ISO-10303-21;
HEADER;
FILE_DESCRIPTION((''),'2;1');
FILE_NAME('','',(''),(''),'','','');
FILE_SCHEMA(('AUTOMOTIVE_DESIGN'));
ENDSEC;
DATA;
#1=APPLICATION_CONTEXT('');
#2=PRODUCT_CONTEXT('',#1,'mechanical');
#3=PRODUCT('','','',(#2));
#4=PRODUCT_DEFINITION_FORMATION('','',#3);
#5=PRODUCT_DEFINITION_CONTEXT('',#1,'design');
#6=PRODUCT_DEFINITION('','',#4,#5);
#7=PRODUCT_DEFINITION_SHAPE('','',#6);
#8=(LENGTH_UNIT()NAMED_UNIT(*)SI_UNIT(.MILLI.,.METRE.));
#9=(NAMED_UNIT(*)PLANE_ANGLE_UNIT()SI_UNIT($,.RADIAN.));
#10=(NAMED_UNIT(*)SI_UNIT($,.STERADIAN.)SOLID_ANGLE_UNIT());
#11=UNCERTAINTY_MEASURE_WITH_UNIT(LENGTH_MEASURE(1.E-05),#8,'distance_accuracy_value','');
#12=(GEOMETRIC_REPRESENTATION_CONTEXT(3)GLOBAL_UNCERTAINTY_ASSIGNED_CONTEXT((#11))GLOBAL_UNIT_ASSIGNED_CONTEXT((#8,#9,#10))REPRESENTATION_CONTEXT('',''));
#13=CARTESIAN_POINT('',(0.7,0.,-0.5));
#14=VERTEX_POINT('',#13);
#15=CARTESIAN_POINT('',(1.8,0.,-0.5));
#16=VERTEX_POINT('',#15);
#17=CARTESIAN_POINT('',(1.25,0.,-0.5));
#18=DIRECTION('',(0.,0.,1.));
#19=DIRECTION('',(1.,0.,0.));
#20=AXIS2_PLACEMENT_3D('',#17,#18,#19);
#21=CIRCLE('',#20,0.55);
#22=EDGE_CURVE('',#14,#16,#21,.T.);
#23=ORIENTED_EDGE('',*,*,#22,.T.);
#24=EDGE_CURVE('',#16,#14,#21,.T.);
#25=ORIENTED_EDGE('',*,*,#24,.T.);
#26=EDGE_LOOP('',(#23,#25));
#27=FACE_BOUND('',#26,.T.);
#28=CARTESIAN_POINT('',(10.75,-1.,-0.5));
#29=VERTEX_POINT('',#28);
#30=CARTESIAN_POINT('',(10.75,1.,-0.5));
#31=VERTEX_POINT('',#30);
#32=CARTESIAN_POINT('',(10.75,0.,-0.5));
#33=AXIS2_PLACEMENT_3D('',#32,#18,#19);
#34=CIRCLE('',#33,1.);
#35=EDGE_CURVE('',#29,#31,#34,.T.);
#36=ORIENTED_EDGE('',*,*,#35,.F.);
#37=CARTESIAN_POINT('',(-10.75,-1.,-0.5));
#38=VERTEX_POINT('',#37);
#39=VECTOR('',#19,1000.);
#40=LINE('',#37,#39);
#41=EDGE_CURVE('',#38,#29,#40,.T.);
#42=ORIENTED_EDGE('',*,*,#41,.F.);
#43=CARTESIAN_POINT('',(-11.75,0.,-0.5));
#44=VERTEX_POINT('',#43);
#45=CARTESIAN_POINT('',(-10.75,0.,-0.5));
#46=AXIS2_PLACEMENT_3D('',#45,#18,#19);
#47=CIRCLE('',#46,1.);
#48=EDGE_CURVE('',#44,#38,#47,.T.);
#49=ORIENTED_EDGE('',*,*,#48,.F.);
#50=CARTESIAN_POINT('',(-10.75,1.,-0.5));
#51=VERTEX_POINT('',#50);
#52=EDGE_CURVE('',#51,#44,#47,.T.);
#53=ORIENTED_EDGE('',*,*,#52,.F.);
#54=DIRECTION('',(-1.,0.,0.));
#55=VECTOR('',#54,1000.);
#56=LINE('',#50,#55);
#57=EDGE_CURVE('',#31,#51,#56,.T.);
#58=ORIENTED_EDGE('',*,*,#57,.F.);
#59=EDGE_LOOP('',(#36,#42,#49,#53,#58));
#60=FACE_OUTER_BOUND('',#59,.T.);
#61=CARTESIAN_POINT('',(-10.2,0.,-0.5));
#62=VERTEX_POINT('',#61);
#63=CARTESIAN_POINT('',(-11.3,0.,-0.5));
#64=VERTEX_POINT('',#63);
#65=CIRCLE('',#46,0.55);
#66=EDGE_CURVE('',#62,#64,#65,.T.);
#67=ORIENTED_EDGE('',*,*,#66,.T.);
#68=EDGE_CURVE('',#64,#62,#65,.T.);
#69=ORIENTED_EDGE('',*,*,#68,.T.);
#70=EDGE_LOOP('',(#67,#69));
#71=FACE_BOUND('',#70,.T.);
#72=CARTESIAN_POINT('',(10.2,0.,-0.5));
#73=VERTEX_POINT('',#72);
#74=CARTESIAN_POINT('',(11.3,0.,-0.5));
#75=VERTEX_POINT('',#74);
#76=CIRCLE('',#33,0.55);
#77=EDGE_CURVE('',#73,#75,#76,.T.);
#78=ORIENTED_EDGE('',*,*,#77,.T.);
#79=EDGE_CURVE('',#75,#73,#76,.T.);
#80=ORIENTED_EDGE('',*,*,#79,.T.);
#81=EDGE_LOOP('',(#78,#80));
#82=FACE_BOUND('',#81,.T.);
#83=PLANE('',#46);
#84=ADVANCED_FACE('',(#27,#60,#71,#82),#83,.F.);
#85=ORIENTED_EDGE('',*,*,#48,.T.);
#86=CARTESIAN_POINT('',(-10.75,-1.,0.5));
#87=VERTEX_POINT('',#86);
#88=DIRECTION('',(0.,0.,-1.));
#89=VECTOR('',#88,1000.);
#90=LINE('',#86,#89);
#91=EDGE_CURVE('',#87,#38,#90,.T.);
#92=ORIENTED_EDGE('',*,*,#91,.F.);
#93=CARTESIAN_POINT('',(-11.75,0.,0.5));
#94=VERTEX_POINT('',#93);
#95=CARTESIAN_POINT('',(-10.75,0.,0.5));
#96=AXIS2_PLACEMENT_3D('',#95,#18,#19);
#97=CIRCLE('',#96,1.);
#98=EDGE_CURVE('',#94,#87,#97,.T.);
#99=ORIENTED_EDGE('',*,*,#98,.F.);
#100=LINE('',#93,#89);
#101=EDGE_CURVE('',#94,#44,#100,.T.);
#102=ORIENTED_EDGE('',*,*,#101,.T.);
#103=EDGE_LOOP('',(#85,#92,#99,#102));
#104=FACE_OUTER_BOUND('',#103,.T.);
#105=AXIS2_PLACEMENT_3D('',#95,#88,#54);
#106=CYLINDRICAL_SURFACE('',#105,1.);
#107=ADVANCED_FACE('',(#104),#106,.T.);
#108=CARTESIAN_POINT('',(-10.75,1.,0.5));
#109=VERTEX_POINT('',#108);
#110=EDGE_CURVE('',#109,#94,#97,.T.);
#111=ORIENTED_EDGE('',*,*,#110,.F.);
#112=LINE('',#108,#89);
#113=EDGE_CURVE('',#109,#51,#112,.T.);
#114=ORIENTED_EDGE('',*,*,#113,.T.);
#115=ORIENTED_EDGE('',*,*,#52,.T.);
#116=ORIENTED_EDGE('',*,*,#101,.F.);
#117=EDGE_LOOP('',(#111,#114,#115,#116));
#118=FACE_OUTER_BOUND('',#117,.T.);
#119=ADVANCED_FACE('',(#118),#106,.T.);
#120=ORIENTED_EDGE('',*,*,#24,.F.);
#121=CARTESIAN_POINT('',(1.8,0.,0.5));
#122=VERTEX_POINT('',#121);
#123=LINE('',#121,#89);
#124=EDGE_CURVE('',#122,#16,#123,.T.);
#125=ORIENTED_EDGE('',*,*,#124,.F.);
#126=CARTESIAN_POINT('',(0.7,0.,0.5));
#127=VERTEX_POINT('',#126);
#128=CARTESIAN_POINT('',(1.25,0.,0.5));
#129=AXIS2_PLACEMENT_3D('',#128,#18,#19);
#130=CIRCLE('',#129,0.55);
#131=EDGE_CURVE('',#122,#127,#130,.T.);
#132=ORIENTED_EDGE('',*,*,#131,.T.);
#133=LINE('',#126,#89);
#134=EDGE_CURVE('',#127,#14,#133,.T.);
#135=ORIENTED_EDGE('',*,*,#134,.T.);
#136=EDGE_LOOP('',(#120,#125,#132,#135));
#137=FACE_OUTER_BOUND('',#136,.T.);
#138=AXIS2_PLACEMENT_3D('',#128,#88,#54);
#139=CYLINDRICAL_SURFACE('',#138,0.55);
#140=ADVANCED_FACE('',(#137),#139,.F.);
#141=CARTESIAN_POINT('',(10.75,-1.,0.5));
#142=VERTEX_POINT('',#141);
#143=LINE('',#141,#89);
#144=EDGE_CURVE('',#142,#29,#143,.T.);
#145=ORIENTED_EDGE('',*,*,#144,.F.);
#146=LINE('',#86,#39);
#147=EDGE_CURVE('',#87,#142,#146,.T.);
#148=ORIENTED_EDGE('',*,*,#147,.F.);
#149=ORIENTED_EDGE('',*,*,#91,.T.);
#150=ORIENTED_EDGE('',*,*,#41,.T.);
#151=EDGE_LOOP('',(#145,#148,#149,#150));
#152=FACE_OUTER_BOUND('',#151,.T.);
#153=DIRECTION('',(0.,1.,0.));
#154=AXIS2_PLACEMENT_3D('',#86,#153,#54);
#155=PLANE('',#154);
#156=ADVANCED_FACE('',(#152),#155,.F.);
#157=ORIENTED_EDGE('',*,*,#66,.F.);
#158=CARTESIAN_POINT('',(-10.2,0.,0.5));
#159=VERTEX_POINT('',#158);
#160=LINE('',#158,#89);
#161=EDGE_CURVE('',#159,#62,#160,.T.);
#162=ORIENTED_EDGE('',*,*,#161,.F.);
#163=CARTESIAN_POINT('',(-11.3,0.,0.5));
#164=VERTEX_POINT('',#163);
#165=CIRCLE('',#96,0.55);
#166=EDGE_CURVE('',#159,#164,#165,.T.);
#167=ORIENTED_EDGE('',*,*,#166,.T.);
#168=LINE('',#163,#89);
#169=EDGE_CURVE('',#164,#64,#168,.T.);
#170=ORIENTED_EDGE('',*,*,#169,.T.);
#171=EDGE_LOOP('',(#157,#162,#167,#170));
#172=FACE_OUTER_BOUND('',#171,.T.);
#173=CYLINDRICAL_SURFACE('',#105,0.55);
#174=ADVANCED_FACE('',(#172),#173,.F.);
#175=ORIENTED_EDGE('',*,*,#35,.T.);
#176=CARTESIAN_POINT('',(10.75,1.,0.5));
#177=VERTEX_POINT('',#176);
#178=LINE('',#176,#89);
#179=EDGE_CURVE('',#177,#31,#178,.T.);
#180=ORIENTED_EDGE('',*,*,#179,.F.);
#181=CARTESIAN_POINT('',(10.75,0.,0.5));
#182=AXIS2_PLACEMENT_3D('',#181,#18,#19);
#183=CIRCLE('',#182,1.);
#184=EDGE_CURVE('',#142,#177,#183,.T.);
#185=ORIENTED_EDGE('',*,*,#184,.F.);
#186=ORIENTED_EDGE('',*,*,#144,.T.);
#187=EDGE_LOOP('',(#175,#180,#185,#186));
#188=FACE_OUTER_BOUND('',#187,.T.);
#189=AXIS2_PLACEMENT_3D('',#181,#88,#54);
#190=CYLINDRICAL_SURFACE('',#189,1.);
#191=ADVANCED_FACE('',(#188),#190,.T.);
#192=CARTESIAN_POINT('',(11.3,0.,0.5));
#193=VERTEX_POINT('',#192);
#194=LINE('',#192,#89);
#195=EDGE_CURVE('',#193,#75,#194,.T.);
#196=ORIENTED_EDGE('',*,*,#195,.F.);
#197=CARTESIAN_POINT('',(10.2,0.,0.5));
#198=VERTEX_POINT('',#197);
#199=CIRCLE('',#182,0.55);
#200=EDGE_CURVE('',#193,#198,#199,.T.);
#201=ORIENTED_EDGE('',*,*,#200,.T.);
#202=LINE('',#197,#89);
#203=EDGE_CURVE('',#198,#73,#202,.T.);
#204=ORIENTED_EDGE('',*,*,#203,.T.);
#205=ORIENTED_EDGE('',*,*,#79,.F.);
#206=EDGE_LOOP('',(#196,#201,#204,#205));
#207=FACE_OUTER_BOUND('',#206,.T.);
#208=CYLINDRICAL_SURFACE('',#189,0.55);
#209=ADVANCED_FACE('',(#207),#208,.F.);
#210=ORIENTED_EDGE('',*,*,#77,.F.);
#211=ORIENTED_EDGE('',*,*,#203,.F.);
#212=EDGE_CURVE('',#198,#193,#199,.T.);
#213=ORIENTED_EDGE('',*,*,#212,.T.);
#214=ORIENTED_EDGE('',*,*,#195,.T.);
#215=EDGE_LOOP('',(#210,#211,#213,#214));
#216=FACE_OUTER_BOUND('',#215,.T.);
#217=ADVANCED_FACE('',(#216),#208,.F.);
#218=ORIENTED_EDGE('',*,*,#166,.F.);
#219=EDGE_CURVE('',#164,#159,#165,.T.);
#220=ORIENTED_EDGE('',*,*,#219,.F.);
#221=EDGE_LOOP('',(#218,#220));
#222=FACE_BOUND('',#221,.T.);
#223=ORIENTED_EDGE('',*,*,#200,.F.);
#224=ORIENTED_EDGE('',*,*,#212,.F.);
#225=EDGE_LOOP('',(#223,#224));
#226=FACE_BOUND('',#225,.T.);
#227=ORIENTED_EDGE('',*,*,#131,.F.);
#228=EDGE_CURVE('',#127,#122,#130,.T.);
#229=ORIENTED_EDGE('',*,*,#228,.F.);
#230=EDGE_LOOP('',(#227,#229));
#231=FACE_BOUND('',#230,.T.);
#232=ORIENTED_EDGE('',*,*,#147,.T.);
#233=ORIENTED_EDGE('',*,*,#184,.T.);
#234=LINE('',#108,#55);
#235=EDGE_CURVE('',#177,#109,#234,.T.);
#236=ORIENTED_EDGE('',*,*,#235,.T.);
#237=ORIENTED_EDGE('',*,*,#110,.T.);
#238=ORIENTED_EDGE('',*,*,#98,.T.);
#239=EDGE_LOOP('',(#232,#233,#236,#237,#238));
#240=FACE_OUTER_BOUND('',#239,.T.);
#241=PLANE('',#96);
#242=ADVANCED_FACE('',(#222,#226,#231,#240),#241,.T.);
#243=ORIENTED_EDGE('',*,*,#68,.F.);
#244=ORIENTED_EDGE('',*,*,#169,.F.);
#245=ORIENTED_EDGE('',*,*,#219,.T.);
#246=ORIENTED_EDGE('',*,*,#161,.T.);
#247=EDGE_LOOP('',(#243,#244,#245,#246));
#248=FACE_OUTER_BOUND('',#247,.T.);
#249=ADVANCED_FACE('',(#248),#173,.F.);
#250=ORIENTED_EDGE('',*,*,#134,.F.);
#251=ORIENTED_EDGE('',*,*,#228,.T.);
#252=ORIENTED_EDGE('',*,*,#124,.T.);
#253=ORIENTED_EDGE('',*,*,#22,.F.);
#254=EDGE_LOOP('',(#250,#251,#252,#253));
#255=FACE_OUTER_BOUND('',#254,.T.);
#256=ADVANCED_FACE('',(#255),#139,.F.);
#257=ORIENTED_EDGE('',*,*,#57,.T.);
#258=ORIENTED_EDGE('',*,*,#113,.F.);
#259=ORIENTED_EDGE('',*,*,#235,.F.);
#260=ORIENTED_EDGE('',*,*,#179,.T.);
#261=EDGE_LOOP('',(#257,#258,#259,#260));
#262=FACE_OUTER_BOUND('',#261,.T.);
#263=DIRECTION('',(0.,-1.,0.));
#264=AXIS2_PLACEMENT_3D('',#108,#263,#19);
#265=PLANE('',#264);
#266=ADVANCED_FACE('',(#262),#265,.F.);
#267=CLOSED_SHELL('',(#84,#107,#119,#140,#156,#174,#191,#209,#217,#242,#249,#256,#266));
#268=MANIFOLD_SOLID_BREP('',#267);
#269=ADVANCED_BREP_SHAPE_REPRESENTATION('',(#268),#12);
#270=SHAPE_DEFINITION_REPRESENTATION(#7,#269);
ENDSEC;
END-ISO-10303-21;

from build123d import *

# Parameters (mm, degrees)
SKETCH1_R           = 0.55
THIGH1_LENGTH_DEPTH = 0.5


with BuildPart() as part:
    # Sketch1 → Thigh1 length (new, symmetric)
    with BuildSketch(Plane.XY):
        with BuildLine():
            Line((-10.75, 1), (10.75, 1))
            ThreePointArc((10.75, 1), (11.75, 0), (10.75, -1))
            Line((10.75, -1), (-10.75, -1))
            ThreePointArc((-10.75, -1), (-11.75, 0), (-10.75, 1))
        make_face()
        with Locations((-10.75, 0)):
            Circle(SKETCH1_R, mode=Mode.SUBTRACT)
        with Locations((10.75, 0)):
            Circle(SKETCH1_R, mode=Mode.SUBTRACT)
        with Locations((1.25, 0)):
            Circle(SKETCH1_R, mode=Mode.SUBTRACT)
    extrude(amount=THIGH1_LENGTH_DEPTH, both=True)


solid = part.part
